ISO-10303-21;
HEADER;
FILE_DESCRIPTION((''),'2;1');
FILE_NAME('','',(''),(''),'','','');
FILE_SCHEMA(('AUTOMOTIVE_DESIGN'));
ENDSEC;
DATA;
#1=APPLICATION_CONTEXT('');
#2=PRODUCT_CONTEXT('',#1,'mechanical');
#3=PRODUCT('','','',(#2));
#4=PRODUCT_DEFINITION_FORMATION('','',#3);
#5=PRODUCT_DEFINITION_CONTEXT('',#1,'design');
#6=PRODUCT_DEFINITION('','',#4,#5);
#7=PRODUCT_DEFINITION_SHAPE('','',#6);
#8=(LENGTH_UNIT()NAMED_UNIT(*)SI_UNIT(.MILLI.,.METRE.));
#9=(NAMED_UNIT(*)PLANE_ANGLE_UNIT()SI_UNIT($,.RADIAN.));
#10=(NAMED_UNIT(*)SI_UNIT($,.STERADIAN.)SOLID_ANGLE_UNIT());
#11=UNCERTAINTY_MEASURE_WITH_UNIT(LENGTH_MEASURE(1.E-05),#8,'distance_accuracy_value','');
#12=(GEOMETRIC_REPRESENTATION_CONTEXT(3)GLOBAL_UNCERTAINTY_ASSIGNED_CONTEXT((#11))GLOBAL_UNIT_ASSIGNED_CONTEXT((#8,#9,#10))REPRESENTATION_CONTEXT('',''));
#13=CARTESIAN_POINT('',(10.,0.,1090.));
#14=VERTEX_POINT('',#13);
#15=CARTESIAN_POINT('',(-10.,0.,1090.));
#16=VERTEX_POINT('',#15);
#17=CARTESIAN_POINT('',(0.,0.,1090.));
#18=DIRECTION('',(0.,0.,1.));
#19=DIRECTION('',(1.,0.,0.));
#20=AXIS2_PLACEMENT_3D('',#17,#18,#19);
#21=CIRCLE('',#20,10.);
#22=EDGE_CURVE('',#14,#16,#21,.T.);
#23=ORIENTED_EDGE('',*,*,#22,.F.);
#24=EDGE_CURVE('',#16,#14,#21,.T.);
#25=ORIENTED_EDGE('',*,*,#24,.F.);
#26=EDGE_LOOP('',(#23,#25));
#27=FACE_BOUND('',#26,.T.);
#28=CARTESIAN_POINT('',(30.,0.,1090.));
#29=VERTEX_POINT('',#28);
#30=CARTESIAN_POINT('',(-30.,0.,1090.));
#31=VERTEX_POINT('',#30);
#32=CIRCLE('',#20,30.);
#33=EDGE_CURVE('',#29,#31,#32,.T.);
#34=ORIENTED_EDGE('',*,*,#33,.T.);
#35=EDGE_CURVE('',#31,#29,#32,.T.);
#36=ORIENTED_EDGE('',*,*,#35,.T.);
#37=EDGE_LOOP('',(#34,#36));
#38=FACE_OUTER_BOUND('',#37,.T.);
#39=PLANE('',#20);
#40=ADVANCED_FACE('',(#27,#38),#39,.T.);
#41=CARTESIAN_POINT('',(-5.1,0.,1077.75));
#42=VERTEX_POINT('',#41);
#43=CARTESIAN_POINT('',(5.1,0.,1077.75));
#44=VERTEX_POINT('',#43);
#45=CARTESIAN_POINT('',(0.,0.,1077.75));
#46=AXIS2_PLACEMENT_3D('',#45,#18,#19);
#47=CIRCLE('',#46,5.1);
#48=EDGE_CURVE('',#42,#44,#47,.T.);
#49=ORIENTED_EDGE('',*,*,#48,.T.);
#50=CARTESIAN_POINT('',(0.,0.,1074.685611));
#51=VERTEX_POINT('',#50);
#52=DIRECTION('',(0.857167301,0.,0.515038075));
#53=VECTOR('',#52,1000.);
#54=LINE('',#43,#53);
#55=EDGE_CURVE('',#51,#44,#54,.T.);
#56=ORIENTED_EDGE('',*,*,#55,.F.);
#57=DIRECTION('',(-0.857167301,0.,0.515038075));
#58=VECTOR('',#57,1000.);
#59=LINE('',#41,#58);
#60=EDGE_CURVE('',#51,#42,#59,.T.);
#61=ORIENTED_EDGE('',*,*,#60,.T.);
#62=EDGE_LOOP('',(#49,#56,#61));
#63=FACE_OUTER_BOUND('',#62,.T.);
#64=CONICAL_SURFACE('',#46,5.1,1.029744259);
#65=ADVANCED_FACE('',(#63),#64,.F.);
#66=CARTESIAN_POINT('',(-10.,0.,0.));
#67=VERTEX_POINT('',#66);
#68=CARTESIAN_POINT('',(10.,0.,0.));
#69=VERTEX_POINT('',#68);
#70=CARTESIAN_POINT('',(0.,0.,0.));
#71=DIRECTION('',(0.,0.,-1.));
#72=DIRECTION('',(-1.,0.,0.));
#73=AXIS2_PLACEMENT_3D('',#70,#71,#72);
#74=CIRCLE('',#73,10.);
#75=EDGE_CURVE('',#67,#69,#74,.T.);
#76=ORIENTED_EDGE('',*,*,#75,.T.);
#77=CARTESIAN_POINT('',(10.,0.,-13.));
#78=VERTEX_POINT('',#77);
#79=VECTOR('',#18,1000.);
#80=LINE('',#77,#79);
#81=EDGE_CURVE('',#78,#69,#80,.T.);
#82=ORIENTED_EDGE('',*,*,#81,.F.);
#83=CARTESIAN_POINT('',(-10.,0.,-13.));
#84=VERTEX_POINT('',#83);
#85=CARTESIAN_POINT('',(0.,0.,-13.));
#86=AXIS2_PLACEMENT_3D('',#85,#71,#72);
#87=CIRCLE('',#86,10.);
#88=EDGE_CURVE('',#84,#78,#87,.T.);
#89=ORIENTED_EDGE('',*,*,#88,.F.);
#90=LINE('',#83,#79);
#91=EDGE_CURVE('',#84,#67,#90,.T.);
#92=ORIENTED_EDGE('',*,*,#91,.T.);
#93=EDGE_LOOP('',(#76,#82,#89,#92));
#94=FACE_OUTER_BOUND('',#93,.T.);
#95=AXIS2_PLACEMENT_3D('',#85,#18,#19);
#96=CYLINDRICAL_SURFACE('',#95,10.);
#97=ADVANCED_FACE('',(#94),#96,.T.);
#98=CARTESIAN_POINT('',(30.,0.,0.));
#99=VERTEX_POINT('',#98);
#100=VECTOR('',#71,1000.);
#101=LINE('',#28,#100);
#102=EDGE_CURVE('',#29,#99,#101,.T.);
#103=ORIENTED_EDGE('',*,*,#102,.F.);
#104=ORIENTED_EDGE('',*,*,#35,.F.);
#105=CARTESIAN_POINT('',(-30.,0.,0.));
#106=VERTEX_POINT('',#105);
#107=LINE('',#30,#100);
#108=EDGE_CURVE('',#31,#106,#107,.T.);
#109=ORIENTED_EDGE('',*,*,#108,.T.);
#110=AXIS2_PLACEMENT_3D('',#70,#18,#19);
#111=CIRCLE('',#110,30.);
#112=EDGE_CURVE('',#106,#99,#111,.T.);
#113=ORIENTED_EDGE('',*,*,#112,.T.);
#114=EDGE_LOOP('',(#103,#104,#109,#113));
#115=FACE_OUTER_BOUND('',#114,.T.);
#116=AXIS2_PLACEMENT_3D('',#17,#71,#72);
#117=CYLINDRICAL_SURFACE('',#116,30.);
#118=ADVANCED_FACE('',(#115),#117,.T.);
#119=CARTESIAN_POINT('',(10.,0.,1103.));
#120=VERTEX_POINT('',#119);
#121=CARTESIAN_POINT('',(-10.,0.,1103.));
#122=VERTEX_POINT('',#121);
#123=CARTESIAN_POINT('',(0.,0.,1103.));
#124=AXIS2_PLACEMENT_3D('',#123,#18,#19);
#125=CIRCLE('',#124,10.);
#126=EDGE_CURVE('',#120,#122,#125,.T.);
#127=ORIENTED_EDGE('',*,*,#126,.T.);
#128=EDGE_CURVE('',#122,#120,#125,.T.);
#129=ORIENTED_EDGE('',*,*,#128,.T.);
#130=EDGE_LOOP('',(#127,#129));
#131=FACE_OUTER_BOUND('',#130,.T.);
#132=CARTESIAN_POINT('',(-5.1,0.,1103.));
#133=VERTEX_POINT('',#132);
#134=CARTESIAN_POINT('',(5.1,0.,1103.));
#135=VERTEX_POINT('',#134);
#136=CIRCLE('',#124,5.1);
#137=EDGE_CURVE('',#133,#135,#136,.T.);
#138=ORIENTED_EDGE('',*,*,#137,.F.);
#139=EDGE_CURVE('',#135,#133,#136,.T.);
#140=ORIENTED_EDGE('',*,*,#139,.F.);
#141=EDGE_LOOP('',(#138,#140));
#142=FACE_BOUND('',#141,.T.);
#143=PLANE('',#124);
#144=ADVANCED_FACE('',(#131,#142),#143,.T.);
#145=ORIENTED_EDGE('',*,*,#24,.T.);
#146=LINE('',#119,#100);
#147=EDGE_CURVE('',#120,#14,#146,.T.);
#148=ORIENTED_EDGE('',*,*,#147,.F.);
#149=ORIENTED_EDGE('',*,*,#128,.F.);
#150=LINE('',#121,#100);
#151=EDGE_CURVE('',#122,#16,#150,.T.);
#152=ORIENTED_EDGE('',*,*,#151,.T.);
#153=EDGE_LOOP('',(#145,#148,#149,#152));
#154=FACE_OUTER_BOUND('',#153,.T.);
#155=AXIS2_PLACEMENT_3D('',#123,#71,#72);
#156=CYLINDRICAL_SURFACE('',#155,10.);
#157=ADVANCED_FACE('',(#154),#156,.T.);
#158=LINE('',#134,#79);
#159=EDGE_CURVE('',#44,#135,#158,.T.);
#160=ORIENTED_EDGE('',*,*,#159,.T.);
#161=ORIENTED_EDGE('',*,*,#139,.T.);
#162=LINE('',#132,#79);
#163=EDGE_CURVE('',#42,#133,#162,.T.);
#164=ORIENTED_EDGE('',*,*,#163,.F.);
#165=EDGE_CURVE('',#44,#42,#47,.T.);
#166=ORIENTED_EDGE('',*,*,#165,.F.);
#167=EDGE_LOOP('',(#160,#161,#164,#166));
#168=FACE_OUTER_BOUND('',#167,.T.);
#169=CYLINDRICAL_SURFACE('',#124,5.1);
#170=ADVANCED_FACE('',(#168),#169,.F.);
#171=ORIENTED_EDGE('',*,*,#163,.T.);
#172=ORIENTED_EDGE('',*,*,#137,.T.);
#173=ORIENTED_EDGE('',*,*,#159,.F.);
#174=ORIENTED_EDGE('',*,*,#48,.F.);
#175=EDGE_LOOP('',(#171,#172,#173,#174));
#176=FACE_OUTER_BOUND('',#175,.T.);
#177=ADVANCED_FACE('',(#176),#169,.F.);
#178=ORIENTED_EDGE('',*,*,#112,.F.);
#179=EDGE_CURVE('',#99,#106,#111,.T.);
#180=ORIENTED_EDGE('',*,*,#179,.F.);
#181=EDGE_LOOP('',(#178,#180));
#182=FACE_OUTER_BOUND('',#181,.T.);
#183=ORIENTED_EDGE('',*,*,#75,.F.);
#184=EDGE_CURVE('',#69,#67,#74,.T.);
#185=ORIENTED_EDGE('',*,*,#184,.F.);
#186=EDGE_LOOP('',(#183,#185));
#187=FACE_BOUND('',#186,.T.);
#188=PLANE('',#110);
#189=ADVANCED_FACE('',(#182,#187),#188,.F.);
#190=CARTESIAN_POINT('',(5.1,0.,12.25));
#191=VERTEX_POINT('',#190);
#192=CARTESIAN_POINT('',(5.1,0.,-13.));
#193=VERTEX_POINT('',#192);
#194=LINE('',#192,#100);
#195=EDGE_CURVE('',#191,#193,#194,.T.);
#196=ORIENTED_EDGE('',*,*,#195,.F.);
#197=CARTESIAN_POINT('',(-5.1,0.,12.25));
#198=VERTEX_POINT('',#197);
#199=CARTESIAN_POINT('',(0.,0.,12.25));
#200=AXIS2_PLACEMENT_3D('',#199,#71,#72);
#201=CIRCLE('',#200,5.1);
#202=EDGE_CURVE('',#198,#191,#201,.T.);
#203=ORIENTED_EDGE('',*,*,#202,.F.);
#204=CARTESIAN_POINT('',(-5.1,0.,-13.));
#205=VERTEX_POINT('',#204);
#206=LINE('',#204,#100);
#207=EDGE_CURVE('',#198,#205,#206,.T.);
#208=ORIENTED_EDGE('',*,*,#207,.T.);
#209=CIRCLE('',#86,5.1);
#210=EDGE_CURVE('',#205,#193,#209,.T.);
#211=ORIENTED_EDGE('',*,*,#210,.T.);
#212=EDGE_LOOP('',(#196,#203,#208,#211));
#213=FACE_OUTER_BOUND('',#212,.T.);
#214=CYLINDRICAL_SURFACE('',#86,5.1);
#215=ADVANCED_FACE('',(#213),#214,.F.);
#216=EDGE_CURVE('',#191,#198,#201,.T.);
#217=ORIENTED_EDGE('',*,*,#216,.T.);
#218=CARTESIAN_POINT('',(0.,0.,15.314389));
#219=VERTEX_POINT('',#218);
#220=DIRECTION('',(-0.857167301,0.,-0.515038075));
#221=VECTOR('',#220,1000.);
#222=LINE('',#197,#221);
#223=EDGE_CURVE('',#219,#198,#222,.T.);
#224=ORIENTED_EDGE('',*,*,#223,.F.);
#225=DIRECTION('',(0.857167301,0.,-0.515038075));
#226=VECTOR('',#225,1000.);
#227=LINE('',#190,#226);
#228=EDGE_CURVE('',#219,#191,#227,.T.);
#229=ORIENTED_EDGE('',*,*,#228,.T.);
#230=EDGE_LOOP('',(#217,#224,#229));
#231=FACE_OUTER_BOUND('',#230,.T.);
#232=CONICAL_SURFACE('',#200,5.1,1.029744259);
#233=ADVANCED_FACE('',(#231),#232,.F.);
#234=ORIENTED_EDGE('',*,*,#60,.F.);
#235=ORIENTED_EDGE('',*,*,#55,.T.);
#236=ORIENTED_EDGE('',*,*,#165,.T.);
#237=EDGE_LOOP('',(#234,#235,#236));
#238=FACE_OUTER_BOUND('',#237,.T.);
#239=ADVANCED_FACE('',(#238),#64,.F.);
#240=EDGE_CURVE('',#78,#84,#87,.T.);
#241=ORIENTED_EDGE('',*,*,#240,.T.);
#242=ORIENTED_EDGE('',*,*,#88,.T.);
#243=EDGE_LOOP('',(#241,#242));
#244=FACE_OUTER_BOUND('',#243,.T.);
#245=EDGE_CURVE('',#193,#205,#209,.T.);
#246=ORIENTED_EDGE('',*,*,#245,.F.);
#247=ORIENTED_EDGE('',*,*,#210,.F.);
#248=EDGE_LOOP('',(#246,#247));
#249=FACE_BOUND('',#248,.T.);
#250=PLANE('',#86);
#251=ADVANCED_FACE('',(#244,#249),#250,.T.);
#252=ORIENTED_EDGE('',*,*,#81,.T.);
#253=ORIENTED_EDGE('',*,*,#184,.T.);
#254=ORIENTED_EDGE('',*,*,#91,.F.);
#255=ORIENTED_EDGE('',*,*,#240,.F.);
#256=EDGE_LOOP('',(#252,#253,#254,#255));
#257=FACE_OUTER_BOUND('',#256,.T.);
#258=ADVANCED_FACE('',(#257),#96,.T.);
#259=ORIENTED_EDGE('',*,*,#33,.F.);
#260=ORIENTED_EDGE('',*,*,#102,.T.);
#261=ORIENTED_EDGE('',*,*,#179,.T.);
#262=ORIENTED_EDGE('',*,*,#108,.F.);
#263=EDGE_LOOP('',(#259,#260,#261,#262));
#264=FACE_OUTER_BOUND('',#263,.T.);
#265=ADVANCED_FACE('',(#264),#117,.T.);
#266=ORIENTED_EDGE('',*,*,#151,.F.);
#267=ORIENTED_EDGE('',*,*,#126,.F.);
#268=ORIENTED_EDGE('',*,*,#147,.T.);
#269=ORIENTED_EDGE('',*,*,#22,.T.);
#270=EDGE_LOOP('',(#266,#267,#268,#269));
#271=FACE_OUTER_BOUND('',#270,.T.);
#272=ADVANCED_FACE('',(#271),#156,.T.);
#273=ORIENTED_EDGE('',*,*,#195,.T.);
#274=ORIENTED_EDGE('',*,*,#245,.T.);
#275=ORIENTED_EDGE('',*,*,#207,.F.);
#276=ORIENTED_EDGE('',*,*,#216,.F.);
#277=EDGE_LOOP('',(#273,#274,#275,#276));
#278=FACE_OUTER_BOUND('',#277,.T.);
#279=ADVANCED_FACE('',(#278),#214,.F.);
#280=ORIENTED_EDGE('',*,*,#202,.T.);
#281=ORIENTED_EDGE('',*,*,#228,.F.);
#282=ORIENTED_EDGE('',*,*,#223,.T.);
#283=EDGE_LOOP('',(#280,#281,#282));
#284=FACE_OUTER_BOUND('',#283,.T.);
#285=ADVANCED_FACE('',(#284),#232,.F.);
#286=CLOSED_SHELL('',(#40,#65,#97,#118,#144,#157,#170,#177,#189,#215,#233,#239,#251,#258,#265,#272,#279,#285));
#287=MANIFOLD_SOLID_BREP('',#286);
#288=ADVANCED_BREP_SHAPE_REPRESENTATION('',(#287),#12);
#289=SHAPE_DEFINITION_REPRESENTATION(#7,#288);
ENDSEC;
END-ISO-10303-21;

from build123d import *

# Parameters (mm, degrees)
SKETCH1_R              = 30
BOSS_EXTRUDE1_DEPTH    = 1090
SKETCH2_R              = 10
BOSS_EXTRUDE2_DEPTH    = 13
BOSS_EXTRUDE3_START    = 13
SKETCH3_R              = 10
BOSS_EXTRUDE3_DEPTH    = 13
M12_TAPPED_HOLE1_D     = 10.2
M12_TAPPED_HOLE1_DEPTH = 25.25
M12_TAPPED_HOLE1_TIP   = 3.064389157
M12_TAPPED_HOLE2_D     = 10.2
M12_TAPPED_HOLE2_DEPTH = 25.25
M12_TAPPED_HOLE2_TIP   = 3.064389157


with BuildPart() as part:
    # Sketch1 → Boss-Extrude1 (new body)
    with BuildSketch(Plane.XY):
        Circle(SKETCH1_R)
    extrude(amount=BOSS_EXTRUDE1_DEPTH)

    # Sketch2 → Boss-Extrude2 (add)
    with BuildSketch(Plane.XY.offset(1090)):
        with Locations(Location((0, 0, 0), (0, 0, 180))):
            Circle(SKETCH2_R)
    extrude(amount=BOSS_EXTRUDE2_DEPTH)

    # Sketch3 → Boss-Extrude3 (add)
    with BuildSketch(Plane(origin=(0, 0, 0), x_dir=(-1, 0, 0), z_dir=(0, 0, -1)).offset(BOSS_EXTRUDE3_START)):
        Circle(SKETCH3_R)
    extrude(amount=-BOSS_EXTRUDE3_DEPTH)

    # M12 Tapped Hole1
    with Locations(Plane(origin=(0, 0, -13), x_dir=(-1, 0, 0), z_dir=(0, 0, -1))):
        with Locations((0, 0)):
            Hole(M12_TAPPED_HOLE1_D / 2, depth=M12_TAPPED_HOLE1_DEPTH)
            with Locations((0, 0, -(M12_TAPPED_HOLE1_DEPTH + M12_TAPPED_HOLE1_TIP / 2))):  # 118° drill point
                Cone(0, M12_TAPPED_HOLE1_D / 2, M12_TAPPED_HOLE1_TIP, mode=Mode.SUBTRACT)

    # M12 Tapped Hole2
    with Locations(Plane.XY.offset(1103)):
        with Locations((0, 0)):
            Hole(M12_TAPPED_HOLE2_D / 2, depth=M12_TAPPED_HOLE2_DEPTH)
            with Locations((0, 0, -(M12_TAPPED_HOLE2_DEPTH + M12_TAPPED_HOLE2_TIP / 2))):  # 118° drill point
                Cone(0, M12_TAPPED_HOLE2_D / 2, M12_TAPPED_HOLE2_TIP, mode=Mode.SUBTRACT)


solid = part.part
